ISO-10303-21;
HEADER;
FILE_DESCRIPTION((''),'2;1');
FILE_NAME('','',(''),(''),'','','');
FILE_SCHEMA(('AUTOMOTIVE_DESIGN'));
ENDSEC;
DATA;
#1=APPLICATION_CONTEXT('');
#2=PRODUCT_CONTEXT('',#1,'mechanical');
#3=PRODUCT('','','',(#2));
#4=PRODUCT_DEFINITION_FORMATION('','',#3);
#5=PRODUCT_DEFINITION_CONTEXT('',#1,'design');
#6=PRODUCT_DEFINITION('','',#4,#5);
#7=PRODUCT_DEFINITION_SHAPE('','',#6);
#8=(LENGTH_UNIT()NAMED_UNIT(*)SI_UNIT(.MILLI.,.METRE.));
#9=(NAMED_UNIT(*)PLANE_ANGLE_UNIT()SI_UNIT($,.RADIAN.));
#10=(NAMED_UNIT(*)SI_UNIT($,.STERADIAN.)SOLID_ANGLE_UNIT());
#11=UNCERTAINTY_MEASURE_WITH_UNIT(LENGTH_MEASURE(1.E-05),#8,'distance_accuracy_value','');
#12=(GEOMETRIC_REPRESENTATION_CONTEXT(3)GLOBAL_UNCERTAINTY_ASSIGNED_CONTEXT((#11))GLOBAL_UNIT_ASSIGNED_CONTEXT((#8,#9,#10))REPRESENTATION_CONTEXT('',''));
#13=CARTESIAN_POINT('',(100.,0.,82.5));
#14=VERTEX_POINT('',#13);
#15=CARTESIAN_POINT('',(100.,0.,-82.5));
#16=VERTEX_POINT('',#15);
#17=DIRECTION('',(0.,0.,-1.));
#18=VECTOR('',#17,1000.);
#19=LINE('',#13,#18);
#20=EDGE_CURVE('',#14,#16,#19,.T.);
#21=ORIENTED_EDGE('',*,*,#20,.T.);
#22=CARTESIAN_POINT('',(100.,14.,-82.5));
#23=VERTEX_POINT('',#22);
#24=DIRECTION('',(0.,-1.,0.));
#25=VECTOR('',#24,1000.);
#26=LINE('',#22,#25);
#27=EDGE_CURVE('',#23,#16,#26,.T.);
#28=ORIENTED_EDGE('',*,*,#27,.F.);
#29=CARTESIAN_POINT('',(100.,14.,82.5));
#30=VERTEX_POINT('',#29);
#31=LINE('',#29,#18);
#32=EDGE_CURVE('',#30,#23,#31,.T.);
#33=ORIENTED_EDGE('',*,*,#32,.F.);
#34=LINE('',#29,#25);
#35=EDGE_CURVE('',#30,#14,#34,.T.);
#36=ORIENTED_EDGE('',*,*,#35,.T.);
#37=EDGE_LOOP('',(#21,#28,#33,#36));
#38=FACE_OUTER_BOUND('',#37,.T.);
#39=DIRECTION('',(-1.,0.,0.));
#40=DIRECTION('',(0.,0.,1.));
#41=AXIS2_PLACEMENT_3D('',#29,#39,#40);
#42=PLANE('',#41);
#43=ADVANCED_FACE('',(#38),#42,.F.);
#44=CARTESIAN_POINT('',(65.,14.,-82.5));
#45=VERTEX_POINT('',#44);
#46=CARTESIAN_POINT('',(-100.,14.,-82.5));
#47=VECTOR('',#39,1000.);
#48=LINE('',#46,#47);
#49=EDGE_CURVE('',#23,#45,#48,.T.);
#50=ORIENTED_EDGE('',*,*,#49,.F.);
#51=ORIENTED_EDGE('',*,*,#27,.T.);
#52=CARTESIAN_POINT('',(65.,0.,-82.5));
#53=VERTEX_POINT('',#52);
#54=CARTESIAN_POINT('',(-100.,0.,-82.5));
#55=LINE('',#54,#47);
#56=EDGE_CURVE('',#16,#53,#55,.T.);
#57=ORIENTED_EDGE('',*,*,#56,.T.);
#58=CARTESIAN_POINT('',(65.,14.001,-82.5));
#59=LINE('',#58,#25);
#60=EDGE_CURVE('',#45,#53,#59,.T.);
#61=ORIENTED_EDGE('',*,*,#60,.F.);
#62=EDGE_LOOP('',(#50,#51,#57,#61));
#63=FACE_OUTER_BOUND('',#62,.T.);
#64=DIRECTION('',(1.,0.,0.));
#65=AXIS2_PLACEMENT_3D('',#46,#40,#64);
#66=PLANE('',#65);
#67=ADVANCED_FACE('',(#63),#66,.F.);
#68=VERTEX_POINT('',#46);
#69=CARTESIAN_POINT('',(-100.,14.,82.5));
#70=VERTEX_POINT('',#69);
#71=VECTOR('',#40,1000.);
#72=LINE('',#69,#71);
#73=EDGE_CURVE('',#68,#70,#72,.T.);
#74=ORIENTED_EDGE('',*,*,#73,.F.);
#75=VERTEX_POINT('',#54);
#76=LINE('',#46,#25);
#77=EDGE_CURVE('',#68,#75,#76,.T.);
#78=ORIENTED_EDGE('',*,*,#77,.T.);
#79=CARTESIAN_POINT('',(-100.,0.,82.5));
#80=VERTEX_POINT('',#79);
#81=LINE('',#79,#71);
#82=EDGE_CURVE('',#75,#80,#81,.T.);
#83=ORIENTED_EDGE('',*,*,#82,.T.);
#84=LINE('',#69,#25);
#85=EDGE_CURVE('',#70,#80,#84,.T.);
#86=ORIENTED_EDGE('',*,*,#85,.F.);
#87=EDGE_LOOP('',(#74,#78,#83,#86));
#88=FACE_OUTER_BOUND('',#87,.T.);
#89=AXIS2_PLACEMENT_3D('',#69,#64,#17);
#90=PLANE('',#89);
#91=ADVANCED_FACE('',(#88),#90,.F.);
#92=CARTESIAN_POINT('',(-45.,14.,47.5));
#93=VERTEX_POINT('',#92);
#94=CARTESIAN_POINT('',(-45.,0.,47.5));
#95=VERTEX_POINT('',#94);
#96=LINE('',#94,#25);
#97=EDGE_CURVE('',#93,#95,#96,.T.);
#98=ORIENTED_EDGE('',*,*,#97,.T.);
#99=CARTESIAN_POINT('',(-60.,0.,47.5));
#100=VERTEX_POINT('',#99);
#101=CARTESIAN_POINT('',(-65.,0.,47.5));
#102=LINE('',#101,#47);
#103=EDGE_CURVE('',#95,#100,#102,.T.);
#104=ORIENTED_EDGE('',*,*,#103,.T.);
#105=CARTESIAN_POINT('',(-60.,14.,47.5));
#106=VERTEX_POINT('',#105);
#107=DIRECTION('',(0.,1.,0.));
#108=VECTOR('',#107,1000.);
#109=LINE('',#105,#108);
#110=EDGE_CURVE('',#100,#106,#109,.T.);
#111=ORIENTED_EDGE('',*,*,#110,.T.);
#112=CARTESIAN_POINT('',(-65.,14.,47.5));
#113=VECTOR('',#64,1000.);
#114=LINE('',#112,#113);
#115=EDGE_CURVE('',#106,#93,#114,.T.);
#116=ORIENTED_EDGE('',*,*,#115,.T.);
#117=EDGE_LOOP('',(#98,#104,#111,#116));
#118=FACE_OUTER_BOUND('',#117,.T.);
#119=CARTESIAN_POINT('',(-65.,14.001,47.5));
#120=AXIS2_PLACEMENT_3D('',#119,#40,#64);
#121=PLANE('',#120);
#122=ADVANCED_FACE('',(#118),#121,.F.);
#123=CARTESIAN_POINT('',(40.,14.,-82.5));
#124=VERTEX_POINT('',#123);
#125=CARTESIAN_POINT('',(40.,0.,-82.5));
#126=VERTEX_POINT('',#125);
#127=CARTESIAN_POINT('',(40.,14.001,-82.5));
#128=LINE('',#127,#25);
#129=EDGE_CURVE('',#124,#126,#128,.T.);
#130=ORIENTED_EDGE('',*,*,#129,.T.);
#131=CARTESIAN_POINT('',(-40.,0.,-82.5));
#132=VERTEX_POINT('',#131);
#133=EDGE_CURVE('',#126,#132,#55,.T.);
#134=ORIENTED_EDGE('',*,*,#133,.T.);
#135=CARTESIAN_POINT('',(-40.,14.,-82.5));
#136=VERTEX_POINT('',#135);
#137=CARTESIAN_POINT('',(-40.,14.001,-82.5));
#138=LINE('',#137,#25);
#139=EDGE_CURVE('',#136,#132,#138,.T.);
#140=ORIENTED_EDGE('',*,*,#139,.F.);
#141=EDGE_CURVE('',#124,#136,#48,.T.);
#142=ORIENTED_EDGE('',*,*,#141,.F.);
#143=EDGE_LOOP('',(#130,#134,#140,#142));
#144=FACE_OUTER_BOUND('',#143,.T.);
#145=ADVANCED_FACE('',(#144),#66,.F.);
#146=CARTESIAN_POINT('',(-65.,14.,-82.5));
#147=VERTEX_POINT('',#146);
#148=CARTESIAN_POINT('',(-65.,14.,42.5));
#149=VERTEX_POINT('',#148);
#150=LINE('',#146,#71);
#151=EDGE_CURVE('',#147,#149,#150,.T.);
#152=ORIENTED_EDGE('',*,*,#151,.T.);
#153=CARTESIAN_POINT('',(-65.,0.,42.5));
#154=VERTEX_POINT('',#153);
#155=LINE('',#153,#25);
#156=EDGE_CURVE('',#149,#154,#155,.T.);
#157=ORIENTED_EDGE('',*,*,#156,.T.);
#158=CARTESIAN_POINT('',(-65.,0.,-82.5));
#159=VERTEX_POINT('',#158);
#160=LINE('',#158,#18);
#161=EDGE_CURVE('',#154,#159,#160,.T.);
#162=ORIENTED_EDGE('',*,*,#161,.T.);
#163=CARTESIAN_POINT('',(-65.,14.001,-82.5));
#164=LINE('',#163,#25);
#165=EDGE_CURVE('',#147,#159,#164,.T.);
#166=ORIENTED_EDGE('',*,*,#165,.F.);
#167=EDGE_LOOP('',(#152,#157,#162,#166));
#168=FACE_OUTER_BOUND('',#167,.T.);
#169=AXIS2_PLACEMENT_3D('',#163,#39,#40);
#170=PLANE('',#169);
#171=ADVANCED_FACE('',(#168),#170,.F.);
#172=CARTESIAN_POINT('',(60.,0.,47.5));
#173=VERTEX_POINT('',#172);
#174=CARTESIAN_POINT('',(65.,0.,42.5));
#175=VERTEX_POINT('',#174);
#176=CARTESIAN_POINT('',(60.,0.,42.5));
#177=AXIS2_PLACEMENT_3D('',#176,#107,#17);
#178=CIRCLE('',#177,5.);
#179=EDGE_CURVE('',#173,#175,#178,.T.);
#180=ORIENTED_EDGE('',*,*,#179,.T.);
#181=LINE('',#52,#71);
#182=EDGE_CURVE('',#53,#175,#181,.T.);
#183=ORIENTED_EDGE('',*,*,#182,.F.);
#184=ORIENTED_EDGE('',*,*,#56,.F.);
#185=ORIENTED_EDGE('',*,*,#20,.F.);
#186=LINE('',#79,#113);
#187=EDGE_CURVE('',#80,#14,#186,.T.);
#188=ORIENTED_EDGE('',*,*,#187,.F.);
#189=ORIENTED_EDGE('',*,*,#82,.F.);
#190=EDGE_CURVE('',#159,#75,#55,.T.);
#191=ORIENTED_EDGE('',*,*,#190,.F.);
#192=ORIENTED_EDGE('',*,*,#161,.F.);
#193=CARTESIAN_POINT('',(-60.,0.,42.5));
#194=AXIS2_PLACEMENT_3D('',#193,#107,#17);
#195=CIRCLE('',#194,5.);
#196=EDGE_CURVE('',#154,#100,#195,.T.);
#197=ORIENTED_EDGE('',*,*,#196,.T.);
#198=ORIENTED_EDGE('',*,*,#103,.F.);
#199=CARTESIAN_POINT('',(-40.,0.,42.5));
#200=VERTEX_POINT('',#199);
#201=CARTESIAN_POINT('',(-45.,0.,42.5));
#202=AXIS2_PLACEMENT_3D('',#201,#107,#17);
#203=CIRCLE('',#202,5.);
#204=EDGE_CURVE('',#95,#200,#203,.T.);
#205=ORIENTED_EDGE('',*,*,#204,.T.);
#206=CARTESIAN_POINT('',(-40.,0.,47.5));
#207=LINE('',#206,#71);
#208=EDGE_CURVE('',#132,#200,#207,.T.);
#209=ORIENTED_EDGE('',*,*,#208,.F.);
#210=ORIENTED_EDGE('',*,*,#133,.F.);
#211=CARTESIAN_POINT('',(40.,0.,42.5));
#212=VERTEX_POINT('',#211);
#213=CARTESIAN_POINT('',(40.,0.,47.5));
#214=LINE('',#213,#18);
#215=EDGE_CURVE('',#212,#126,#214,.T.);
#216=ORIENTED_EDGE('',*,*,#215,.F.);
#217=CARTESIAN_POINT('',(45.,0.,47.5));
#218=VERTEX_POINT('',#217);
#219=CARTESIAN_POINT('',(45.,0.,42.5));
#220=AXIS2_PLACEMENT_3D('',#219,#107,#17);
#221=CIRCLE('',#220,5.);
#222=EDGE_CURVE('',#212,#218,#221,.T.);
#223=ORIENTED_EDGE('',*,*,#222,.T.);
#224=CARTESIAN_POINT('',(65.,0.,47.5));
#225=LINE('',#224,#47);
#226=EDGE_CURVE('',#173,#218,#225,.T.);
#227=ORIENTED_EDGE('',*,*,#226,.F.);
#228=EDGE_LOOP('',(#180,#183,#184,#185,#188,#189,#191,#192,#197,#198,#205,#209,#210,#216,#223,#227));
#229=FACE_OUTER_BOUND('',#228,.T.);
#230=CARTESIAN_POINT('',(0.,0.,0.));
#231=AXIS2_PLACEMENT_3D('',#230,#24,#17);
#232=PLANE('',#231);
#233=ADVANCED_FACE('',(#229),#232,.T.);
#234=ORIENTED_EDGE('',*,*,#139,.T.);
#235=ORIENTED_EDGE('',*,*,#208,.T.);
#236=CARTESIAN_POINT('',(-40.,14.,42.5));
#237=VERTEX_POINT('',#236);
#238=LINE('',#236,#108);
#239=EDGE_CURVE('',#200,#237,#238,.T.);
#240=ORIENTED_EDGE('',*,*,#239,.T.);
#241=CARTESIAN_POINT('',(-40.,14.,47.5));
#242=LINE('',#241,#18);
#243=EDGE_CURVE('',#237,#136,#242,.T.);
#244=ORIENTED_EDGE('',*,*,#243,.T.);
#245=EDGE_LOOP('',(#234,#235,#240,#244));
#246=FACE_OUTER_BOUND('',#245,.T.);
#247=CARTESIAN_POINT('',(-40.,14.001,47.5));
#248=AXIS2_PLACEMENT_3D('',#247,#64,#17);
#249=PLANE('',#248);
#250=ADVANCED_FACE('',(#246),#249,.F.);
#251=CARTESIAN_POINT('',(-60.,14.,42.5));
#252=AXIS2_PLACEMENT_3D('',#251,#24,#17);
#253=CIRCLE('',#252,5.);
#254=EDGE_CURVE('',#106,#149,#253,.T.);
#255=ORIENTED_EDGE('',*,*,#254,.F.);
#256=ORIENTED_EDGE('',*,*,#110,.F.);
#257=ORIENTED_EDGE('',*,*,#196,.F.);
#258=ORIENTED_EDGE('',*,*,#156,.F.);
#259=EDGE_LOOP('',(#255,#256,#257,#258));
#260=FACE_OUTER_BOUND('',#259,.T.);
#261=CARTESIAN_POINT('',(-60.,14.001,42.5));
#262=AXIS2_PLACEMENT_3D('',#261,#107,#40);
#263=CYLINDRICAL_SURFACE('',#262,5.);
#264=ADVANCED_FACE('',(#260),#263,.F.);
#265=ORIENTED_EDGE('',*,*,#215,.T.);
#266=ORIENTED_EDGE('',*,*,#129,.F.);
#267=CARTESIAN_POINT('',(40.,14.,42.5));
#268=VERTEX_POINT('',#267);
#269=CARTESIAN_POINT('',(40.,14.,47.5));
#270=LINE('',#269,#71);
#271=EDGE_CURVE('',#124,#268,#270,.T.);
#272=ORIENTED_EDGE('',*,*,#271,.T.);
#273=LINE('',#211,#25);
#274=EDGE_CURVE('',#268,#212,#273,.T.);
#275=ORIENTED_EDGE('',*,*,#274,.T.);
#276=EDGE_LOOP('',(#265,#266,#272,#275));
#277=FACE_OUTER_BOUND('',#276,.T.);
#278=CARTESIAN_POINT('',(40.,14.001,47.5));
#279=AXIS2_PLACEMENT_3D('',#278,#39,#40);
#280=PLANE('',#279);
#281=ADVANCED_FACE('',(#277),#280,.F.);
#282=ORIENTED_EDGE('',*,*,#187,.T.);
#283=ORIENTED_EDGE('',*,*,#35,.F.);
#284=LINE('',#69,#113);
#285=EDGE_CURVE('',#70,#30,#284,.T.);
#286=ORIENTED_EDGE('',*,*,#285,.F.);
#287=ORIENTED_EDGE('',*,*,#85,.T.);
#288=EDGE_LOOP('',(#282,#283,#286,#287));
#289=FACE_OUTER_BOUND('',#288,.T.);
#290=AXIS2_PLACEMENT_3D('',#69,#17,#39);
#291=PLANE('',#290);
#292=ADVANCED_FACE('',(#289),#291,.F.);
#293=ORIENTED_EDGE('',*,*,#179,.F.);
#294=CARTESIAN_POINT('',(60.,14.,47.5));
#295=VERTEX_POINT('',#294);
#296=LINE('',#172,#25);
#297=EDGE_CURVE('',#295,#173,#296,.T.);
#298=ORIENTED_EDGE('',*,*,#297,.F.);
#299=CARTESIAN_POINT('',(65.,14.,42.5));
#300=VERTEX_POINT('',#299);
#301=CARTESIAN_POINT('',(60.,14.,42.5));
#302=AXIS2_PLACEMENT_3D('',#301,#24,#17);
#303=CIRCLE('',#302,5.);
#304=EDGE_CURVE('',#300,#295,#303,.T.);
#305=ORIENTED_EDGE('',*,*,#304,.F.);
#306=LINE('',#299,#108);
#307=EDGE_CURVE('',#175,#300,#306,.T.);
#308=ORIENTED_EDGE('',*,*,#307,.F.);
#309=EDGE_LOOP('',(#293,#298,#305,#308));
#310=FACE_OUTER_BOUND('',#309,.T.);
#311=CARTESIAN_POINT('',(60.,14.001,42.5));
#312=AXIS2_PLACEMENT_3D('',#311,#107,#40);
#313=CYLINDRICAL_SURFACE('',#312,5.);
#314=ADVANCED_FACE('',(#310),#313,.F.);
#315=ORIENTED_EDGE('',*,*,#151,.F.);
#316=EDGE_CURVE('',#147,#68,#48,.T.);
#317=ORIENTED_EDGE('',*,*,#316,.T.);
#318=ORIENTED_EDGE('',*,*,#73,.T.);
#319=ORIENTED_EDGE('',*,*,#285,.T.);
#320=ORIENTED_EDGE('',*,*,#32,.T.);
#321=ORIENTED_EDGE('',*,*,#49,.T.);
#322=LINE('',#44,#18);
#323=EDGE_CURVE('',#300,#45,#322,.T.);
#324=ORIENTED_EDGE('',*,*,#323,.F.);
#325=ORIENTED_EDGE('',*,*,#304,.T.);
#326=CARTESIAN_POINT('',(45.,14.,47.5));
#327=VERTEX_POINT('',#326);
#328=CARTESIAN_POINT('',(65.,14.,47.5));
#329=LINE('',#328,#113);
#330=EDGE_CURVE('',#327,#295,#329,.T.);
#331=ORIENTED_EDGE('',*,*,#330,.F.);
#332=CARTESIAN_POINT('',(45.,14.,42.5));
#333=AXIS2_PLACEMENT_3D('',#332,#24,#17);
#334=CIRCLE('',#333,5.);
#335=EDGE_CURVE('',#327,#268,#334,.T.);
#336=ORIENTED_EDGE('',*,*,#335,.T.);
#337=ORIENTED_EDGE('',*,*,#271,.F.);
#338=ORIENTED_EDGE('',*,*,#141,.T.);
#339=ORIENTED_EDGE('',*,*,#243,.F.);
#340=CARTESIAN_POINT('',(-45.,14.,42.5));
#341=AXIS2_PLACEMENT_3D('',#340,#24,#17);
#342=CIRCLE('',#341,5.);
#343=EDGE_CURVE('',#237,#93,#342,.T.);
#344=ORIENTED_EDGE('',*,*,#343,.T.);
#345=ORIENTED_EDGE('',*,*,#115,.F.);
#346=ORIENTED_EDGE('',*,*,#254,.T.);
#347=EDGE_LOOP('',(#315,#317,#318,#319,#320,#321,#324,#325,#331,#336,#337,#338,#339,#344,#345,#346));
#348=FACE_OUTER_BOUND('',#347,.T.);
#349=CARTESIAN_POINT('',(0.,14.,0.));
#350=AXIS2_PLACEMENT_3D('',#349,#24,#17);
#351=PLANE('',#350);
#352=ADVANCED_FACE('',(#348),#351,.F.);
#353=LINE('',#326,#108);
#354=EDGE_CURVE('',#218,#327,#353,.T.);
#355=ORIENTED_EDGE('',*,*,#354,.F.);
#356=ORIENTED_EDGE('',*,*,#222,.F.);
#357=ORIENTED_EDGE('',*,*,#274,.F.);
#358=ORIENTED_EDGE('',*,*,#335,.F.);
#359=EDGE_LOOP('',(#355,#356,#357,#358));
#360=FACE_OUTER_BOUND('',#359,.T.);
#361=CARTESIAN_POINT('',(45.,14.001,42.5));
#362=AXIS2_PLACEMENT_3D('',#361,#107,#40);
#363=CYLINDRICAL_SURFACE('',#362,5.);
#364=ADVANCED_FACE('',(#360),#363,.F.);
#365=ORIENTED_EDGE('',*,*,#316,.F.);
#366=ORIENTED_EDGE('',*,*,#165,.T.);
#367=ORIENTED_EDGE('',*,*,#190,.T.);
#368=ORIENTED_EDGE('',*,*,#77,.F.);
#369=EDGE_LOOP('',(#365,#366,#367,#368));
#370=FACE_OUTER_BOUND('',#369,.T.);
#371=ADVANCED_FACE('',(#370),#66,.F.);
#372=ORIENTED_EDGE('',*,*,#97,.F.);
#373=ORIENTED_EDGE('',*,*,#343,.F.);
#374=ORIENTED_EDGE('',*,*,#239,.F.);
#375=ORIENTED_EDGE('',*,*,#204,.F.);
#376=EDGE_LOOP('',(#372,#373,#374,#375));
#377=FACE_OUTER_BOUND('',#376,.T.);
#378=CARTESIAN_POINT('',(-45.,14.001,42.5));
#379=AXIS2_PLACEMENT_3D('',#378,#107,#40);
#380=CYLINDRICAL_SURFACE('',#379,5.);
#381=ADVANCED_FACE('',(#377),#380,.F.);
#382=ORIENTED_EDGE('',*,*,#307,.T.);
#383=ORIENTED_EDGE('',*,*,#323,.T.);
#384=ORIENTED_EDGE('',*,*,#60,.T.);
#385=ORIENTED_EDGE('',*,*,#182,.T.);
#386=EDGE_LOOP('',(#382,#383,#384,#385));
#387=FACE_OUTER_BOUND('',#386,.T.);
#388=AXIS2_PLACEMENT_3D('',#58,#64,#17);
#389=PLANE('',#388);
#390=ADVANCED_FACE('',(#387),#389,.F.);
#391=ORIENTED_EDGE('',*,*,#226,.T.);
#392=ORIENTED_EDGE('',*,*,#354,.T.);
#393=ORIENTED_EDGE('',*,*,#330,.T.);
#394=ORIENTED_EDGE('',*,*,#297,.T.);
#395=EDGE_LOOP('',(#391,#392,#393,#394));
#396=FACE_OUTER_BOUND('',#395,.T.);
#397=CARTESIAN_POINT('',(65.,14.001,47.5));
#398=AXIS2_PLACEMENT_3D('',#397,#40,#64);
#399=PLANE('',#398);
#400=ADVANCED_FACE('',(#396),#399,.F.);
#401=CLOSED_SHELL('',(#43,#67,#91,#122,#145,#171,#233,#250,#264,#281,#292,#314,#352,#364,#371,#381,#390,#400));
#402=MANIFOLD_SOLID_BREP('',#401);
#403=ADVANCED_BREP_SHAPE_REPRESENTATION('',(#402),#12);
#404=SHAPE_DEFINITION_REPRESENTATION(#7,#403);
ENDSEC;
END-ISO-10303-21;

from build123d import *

# Parameters (mm, degrees)
SKETCH_1_W          = 200
SKETCH_1_H          = 165
EXTRUDE_1_DEPTH     = 14
CUT_EXTRUDE_1_REACH = 132.393
SKETCH_2_W          = 25
SKETCH_2_H          = 130
FILLET_1_R          = 5


with BuildPart() as part:
    # 草图1 → 凸台-拉伸1 (new body)
    with BuildSketch(Plane(origin=(0, 0, 0), x_dir=(1, 0, 0), z_dir=(0, 1, 0))):
        Rectangle(SKETCH_1_W, SKETCH_1_H)
    extrude(amount=EXTRUDE_1_DEPTH)

    # 草图2 → 切除-拉伸1 (cut, up to next)
    with BuildSketch(Plane.XZ, mode=Mode.PRIVATE) as cut_extrude_1_sk1:
        with Locations((52.5, -17.5)):
            Rectangle(SKETCH_2_W, SKETCH_2_H)
    cut_extrude_1_tool1 = extrude(cut_extrude_1_sk1.sketch, amount=-CUT_EXTRUDE_1_REACH, mode=Mode.PRIVATE) & part.part
    # 草图2 → 切除-拉伸1 (cut, up to next)
    with BuildSketch(Plane.XZ, mode=Mode.PRIVATE) as cut_extrude_1_sk2:
        with Locations((-52.5, -17.5)):
            Rectangle(SKETCH_2_W, SKETCH_2_H)
    cut_extrude_1_tool2 = extrude(cut_extrude_1_sk2.sketch, amount=-CUT_EXTRUDE_1_REACH, mode=Mode.PRIVATE) & part.part
    add(cut_extrude_1_tool1.solids().sort_by_distance((52.5, 0, -17.5))[0], mode=Mode.SUBTRACT)
    add(cut_extrude_1_tool2.solids().sort_by_distance((-52.5, 0, -17.5))[0], mode=Mode.SUBTRACT)

    # 圆角1
    fillet_1_edges = [part.edges().sort_by_distance(p)[0] for p in [
        (40, 7, 47.5),
        (65, 7, 47.5),
        (-40, 7, 47.5),
        (-65, 7, 47.5),
    ]]
    fillet(fillet_1_edges, radius=FILLET_1_R)


solid = part.part
